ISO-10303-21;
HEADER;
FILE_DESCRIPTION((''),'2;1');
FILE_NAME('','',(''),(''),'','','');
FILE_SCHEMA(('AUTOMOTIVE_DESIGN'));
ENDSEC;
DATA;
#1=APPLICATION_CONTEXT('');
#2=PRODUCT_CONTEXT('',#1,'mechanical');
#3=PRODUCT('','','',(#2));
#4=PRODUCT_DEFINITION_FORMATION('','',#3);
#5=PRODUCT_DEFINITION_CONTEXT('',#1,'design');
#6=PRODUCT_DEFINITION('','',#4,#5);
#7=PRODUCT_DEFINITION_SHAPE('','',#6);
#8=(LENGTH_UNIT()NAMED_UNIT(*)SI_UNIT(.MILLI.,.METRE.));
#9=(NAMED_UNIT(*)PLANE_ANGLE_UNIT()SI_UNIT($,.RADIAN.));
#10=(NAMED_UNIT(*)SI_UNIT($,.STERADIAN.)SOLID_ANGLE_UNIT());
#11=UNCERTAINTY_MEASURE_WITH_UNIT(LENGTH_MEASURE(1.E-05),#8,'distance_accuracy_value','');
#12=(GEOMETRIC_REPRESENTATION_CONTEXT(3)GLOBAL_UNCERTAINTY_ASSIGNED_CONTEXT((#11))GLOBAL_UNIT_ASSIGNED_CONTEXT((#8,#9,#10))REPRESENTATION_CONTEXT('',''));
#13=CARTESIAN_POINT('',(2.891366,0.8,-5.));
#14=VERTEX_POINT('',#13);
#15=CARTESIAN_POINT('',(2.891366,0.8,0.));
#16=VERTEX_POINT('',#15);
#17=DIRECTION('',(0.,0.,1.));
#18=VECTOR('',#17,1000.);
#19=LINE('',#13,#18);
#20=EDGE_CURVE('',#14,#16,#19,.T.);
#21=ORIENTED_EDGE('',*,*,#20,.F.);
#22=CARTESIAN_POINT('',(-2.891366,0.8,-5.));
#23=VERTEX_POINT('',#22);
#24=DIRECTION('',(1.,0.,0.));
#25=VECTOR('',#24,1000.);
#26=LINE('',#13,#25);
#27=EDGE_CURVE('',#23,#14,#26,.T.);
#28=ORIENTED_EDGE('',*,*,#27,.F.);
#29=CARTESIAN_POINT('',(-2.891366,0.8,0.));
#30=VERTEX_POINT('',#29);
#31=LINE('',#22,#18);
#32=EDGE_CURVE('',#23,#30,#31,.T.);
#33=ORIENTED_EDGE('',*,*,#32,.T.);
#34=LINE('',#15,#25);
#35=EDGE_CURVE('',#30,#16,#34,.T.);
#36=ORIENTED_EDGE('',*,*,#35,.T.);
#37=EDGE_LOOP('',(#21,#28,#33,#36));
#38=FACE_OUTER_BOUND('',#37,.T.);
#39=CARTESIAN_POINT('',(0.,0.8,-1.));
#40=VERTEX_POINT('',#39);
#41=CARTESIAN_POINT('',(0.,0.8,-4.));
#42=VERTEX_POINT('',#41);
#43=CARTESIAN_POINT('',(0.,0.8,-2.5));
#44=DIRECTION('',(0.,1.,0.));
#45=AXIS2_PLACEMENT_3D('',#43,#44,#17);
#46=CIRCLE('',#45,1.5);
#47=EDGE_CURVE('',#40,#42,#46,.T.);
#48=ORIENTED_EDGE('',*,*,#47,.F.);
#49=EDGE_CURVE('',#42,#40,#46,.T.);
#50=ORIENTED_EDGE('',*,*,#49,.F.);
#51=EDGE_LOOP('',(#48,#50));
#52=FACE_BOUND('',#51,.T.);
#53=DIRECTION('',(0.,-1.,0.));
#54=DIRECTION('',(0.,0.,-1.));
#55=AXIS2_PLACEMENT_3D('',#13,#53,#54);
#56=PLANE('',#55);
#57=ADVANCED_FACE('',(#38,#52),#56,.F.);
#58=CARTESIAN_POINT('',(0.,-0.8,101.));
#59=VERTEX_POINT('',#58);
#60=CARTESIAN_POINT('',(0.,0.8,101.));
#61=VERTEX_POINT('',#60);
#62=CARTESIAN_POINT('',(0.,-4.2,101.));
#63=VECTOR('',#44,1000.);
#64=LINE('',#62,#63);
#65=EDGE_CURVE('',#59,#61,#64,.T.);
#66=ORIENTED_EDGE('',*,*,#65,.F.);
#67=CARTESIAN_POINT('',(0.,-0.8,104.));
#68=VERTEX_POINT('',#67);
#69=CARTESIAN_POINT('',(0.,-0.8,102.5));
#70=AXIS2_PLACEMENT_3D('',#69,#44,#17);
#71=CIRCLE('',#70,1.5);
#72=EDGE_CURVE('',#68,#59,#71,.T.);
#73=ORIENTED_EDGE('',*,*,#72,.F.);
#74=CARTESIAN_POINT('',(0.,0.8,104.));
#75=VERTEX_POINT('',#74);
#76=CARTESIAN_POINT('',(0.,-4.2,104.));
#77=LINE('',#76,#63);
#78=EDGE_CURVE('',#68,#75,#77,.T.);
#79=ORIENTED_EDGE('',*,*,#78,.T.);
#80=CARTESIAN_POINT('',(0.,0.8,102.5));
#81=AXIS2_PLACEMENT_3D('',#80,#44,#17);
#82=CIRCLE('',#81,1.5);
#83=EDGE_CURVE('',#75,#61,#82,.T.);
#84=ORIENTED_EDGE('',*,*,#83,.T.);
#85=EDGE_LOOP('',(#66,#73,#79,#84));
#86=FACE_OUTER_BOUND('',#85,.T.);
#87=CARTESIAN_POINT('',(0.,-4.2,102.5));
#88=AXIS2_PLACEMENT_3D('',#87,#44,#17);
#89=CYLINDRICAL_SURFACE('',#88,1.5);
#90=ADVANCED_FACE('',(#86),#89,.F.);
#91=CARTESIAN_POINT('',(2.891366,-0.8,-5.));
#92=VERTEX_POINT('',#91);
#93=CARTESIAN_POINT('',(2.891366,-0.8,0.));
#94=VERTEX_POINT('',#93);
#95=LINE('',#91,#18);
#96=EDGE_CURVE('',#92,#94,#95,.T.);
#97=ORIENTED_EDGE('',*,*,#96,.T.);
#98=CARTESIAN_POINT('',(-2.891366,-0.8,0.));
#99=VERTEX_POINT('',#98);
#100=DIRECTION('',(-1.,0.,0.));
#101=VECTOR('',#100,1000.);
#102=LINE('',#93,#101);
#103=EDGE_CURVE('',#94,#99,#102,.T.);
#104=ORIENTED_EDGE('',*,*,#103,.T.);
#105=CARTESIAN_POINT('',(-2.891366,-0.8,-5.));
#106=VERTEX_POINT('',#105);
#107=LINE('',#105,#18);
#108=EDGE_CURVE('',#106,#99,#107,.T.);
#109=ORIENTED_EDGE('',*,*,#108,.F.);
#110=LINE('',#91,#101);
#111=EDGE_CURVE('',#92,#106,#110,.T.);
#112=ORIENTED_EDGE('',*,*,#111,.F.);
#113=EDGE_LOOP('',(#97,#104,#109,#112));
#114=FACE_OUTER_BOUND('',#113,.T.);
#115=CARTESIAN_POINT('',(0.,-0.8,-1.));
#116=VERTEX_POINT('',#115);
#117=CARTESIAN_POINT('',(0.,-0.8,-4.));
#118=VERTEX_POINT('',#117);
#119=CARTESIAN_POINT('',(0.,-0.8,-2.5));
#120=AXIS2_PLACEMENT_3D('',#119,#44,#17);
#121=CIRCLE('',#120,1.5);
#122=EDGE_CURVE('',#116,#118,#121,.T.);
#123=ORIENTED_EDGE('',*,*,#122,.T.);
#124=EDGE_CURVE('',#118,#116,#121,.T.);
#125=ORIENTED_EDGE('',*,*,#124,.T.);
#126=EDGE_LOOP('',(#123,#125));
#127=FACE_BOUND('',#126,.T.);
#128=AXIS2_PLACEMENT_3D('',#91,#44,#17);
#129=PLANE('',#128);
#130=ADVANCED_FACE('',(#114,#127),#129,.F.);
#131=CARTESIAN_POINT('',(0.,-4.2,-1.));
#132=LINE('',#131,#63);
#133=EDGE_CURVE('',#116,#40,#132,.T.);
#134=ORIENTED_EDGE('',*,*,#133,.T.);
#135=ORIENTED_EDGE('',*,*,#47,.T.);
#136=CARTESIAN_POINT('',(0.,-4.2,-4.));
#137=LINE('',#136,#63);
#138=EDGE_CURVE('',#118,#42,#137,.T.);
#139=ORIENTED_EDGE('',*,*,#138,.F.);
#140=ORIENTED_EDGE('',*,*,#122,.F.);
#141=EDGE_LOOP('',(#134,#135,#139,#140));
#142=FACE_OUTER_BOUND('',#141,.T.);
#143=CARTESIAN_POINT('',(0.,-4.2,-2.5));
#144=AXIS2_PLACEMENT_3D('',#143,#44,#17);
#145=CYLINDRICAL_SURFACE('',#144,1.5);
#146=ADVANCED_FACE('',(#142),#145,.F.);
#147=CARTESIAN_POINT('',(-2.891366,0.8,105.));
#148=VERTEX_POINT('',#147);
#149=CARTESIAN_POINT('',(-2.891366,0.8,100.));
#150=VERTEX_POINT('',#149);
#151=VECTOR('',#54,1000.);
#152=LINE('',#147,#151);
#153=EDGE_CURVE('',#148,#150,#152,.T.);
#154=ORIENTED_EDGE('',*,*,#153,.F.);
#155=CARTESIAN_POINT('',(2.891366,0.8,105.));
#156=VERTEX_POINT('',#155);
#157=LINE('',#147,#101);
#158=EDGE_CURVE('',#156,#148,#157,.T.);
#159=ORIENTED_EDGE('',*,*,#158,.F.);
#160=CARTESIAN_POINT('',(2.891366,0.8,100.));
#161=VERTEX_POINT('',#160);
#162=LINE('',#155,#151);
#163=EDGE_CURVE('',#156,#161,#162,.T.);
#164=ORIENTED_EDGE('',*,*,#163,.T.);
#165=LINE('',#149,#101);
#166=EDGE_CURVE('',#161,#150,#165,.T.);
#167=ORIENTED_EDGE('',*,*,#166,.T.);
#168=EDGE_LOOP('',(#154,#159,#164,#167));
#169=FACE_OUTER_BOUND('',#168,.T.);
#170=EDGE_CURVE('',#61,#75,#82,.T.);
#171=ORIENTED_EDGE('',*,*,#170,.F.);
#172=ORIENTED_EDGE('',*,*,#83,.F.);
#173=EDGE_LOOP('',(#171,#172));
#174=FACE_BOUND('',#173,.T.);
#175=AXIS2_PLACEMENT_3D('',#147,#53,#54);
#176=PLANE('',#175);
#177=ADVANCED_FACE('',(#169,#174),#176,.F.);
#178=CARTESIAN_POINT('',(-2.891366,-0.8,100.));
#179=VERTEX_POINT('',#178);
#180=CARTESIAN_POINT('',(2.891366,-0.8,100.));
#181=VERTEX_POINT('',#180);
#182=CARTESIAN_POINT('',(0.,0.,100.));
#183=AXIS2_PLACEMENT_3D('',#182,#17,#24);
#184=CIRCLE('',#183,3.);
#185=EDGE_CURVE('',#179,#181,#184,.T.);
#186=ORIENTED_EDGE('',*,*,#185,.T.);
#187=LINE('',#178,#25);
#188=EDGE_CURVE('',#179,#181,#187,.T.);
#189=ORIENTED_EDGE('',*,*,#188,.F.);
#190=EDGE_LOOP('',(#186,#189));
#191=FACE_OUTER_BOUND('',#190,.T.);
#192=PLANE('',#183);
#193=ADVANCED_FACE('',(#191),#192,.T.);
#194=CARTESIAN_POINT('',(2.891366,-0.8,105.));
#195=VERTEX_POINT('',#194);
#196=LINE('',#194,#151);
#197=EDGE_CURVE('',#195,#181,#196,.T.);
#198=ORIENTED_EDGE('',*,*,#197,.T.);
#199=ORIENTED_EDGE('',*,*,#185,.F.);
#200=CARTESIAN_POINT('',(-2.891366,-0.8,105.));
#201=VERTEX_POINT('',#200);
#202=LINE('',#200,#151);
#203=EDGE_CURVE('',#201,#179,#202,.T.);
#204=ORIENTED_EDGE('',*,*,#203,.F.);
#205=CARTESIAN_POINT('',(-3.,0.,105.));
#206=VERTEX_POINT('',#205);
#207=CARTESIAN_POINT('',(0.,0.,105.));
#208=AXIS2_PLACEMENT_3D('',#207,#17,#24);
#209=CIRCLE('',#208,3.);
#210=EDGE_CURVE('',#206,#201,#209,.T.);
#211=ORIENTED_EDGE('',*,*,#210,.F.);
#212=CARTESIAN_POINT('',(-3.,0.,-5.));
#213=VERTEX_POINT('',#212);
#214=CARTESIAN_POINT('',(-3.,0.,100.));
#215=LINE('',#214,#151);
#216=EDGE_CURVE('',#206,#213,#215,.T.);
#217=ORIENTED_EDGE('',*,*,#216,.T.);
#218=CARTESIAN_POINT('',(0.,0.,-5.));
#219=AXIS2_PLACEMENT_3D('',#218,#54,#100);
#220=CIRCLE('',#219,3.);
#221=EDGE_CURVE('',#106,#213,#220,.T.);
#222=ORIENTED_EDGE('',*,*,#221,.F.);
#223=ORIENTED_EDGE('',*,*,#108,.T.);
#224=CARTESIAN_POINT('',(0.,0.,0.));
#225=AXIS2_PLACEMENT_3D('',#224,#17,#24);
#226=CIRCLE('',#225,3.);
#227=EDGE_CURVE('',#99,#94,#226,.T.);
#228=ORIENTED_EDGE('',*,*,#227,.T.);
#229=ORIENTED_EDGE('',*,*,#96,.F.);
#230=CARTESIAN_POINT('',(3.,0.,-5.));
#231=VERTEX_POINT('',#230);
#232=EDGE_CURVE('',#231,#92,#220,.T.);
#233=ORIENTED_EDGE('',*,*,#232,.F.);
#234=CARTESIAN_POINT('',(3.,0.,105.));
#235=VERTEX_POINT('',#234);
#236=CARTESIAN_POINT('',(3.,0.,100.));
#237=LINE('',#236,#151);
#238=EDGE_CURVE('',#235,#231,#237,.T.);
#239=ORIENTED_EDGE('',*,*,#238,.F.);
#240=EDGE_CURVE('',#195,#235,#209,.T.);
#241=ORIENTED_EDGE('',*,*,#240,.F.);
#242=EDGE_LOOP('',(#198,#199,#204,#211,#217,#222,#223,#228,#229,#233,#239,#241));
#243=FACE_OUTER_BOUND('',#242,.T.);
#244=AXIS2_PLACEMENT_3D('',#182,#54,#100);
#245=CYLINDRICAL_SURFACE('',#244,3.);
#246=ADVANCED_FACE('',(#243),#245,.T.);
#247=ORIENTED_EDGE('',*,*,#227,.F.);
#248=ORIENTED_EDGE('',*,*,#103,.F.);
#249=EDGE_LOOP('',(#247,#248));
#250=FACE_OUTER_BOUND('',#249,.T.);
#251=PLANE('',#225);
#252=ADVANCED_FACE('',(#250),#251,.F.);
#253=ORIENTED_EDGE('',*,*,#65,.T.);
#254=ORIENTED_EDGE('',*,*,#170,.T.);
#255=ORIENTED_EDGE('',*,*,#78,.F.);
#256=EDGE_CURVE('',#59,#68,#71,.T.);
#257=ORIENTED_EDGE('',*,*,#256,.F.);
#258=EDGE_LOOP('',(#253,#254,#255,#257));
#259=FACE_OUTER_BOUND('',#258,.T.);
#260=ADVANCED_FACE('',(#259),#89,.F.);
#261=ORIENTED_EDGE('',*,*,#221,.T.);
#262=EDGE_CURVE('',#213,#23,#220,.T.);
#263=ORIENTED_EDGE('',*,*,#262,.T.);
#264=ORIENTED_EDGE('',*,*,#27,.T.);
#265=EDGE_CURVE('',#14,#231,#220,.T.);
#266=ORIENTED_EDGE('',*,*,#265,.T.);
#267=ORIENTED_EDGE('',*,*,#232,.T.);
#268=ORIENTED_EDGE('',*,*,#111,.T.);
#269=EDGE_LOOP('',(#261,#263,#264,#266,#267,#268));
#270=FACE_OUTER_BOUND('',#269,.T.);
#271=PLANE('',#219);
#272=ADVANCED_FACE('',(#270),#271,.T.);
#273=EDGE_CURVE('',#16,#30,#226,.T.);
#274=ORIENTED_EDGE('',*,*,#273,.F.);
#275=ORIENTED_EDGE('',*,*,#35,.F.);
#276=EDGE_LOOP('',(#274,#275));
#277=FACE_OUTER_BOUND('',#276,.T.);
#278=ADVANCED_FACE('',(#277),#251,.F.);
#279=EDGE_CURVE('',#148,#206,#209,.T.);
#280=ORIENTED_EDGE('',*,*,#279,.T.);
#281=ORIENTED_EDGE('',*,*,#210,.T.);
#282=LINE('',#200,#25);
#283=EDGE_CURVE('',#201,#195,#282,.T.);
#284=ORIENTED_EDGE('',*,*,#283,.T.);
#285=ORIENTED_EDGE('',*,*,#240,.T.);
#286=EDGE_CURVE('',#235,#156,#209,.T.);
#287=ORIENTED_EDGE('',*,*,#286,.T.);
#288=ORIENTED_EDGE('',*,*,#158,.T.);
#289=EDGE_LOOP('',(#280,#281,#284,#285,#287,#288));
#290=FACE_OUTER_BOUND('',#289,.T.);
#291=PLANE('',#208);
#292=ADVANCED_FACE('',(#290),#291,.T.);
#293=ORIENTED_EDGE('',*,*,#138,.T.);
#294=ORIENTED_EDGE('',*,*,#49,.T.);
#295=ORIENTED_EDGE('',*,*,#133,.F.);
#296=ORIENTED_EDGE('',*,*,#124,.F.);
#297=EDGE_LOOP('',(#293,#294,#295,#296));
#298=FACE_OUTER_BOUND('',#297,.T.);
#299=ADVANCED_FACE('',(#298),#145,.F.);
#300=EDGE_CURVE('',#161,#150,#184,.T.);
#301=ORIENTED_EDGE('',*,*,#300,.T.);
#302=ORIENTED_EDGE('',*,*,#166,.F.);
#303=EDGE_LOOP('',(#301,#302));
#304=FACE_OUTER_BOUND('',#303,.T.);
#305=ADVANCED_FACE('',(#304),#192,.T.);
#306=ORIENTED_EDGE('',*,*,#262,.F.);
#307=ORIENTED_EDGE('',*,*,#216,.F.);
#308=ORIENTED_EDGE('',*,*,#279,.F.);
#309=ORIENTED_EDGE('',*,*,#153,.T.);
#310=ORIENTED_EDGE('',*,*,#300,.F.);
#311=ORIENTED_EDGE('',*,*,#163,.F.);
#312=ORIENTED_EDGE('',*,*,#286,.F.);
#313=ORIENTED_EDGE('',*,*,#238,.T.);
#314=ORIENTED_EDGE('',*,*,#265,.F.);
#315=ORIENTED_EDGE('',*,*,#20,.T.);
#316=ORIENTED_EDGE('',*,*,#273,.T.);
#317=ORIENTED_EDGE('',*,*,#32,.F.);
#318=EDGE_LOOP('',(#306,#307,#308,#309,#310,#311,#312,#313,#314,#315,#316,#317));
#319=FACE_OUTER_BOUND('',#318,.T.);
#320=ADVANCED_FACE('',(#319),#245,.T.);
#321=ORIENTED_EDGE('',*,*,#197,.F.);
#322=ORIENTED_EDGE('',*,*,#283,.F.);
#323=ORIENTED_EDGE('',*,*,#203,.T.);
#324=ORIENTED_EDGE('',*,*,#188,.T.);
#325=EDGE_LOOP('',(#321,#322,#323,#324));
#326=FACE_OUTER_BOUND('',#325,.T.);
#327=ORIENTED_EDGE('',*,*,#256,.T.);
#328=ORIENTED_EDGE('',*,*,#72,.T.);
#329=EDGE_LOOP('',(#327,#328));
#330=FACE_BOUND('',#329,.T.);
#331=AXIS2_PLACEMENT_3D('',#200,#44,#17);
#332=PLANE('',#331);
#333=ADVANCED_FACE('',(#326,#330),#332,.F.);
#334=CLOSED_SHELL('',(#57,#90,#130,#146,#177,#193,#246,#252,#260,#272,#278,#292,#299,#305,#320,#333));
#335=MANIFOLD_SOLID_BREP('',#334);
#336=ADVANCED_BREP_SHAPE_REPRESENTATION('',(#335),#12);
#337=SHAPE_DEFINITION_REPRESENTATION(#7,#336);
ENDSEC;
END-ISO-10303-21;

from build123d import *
from build123d.topology import SkipClean

# Parameters (mm, degrees)
SKETCH_1_R          = 3
EXTRUDE_1_DEPTH     = 100
EXTRUDE_3_DEPTH     = 5
EXTRUDE_START       = 5
EXTRUDE_4_DEPTH     = 5
SKETCH_9_R          = 1.5
CUT_EXTRUDE_1_DEPTH = 5
SKETCH_10_R         = 1.5
CUT_EXTRUDE_2_DEPTH = 5


with BuildPart() as part:
    # 草图1 → 凸台-拉伸1 (new body)
    with BuildSketch(Plane.XY):
        Circle(SKETCH_1_R)
    extrude(amount=EXTRUDE_1_DEPTH)

    # 草图2 → 凸台-拉伸3 (add)
    with SkipClean():  # the faces are left unmerged after this step: merging them gives an invalid solid
        with BuildSketch(Plane.XY.offset(100)):
            with BuildLine():
                Line((-2.891366459, 0.8), (2.891366459, 0.8))
                ThreePointArc((2.891366459, 0.8), (3, 0), (2.891366459, -0.8))
                Line((2.891366459, -0.8), (-2.891366459, -0.8))
                ThreePointArc((-2.891366459, -0.8), (-3, 0), (-2.891366459, 0.8))
            make_face()
        extrude(amount=EXTRUDE_3_DEPTH)

    # 草图8 → 凸台-拉伸4 (add)
    with SkipClean():  # the faces are left unmerged after this step: merging them gives an invalid solid
        with BuildSketch(Plane(origin=(0, 0, 0), x_dir=(-1, 0, 0), z_dir=(0, 0, -1)).offset(EXTRUDE_START)):
            with BuildLine():
                Line((-2.891366459, 0.8), (2.891366459, 0.8))
                ThreePointArc((2.891366459, 0.8), (3, 0), (2.891366459, -0.8))
                Line((2.891366459, -0.8), (-2.891366459, -0.8))
                ThreePointArc((-2.891366459, -0.8), (-3, 0), (-2.891366459, 0.8))
            make_face()
        extrude(amount=-EXTRUDE_4_DEPTH)

    # 草图9 → 切除-拉伸1 (cut)
    with SkipClean():  # the faces are left unmerged after this step: merging them gives an invalid solid
        with BuildSketch(Plane(origin=(0, 0.8, 0), x_dir=(1, 0, 0), z_dir=(0, 1, 0))):
            with Locations(Location((0, 2.5, 0), (0, 0, 270))):
                Circle(SKETCH_9_R)
        extrude(amount=-CUT_EXTRUDE_1_DEPTH, mode=Mode.SUBTRACT)

    # 草图10 → 切除-拉伸2 (cut)
    with SkipClean():  # the faces are left unmerged after this step: merging them gives an invalid solid
        with BuildSketch(Plane(origin=(0, 0.8, 0), x_dir=(1, 0, 0), z_dir=(0, 1, 0))):
            with Locations(Location((0, -102.5, 0), (0, 0, 270))):
                Circle(SKETCH_10_R)
        extrude(amount=-CUT_EXTRUDE_2_DEPTH, mode=Mode.SUBTRACT)


solid = part.part
